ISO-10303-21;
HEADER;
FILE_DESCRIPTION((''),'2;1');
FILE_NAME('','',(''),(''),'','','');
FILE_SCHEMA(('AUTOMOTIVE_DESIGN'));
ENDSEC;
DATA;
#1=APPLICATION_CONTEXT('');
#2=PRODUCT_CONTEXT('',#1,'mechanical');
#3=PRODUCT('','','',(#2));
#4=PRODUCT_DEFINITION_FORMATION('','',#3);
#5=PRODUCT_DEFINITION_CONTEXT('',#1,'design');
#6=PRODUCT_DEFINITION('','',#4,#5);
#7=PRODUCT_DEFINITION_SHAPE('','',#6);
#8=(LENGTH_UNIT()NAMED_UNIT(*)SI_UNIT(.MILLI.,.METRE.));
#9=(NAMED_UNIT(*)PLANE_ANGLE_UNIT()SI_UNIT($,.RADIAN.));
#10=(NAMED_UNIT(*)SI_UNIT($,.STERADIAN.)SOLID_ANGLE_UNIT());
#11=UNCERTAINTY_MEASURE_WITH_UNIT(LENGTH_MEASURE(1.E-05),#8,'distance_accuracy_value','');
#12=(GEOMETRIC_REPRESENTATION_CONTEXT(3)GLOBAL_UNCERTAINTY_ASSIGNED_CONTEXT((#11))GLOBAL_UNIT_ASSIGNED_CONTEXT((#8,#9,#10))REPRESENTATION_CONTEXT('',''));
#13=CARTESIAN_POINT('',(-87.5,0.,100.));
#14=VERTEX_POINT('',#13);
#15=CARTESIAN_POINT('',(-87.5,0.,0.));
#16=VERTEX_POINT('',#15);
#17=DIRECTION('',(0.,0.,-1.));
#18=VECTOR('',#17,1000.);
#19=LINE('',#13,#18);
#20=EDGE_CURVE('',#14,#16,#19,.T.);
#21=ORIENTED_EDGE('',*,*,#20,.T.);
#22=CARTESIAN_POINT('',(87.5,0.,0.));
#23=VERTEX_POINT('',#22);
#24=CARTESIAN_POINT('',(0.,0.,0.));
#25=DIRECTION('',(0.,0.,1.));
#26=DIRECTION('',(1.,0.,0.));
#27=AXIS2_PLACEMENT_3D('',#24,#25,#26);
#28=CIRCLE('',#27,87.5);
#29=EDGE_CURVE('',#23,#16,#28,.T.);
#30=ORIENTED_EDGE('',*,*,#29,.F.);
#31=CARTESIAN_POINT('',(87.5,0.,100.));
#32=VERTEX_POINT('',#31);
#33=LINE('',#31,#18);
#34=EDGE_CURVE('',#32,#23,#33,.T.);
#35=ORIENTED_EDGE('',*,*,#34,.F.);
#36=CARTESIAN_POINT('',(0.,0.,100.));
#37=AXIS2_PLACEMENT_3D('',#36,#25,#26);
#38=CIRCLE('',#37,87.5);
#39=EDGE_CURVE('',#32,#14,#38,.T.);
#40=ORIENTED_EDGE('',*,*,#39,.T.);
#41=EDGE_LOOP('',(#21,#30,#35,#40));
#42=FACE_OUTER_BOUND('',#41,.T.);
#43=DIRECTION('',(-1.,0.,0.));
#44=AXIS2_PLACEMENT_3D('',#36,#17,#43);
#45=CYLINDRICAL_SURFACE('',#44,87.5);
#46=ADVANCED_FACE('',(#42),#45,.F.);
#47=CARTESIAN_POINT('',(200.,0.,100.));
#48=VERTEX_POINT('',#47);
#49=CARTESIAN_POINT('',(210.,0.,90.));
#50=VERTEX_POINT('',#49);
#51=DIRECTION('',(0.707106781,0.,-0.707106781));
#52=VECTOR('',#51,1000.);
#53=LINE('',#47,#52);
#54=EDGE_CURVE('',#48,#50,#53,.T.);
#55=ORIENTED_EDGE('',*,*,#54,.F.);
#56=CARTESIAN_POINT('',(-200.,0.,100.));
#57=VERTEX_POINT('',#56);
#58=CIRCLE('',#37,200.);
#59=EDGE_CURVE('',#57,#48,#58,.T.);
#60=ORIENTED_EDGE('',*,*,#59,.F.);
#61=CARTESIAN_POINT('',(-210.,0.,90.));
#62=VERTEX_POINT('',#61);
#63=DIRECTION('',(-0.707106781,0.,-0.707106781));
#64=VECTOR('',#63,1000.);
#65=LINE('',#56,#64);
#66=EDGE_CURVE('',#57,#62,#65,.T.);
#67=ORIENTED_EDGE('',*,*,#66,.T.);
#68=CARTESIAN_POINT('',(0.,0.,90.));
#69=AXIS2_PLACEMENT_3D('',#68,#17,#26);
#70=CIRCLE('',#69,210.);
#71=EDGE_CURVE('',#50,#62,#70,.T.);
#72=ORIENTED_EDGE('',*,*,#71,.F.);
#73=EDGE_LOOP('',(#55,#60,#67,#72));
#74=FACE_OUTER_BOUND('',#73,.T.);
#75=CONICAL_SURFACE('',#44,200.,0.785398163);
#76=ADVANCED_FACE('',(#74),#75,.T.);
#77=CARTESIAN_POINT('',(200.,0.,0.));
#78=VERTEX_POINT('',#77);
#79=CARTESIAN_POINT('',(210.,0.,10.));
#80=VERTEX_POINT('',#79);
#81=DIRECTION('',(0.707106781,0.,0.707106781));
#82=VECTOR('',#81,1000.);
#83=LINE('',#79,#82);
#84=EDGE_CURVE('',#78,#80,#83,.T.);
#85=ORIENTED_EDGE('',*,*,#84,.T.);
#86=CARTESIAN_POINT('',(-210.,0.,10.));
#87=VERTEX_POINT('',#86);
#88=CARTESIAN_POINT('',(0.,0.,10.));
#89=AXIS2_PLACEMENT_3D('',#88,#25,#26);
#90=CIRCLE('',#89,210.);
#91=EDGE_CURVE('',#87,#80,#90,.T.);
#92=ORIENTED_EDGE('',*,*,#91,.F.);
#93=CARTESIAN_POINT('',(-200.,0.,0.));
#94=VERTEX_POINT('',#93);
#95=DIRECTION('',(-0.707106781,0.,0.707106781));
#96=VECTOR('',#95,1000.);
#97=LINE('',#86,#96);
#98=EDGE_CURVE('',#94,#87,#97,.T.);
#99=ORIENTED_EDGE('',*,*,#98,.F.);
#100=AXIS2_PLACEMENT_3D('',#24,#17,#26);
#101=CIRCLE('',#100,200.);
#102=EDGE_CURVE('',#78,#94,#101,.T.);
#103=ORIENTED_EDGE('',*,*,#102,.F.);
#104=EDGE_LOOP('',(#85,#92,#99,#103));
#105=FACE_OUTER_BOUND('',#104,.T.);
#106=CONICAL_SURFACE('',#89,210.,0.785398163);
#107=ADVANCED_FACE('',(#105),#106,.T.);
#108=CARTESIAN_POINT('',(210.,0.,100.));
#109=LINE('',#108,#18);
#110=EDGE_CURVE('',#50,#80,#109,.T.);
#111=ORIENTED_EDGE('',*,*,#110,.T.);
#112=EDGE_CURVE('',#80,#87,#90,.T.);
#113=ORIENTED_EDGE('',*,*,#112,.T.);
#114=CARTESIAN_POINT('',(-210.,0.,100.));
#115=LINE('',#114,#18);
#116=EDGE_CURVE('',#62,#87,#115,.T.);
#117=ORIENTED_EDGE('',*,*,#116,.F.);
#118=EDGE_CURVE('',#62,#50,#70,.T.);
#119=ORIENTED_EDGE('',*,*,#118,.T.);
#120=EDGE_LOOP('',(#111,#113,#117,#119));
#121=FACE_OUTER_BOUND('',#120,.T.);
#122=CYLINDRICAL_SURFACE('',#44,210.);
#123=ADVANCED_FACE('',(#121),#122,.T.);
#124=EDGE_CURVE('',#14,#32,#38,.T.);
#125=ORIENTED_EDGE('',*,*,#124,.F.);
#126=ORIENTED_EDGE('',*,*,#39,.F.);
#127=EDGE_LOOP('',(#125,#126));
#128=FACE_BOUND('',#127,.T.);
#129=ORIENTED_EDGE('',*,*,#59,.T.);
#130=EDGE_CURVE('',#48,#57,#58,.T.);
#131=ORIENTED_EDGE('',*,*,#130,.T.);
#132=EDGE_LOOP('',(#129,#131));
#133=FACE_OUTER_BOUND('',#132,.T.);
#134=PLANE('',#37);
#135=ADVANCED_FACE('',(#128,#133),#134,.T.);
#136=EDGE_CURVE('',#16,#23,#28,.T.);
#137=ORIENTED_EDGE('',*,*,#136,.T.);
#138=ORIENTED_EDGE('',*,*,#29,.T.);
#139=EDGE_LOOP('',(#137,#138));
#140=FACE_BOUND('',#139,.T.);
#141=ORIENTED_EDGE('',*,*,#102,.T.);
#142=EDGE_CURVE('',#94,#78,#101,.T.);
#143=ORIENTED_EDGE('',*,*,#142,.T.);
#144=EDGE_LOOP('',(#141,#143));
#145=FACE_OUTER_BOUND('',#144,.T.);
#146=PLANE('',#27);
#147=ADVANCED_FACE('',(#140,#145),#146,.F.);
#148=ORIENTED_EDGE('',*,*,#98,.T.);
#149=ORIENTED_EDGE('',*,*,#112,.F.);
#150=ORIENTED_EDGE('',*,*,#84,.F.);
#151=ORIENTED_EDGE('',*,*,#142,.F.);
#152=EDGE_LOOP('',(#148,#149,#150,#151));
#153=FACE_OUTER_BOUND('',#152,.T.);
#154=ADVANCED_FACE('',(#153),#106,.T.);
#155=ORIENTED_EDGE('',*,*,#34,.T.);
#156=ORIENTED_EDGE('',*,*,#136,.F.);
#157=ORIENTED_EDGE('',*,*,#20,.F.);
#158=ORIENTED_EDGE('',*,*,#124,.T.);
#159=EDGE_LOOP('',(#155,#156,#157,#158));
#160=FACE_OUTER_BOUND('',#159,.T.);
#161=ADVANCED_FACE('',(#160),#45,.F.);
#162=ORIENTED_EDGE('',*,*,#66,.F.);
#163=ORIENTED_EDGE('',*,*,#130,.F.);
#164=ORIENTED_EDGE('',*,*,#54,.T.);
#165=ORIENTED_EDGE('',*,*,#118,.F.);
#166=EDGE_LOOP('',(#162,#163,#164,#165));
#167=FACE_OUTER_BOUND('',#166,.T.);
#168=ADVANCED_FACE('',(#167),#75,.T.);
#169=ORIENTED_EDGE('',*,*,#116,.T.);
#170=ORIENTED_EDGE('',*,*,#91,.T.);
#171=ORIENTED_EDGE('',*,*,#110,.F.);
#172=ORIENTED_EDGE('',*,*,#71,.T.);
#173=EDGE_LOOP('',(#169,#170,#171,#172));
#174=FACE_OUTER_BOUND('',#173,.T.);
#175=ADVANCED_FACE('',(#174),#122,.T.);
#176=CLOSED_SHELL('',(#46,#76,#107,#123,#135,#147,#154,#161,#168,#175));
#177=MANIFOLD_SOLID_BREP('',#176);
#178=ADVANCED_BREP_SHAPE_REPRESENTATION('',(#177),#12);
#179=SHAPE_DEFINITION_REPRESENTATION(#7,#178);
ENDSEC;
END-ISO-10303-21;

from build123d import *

# Parameters (mm, degrees)
SKETCH1_R           = 210
SKETCH1_R_2         = 87.5
BOSS_EXTRUDE1_DEPTH = 100
CHAMFER1_SIZE       = 10


with BuildPart() as part:
    # Sketch1 → Boss-Extrude1 (new body)
    with BuildSketch(Plane.XY):
        Circle(SKETCH1_R)
        Circle(SKETCH1_R_2, mode=Mode.SUBTRACT)
    extrude(amount=BOSS_EXTRUDE1_DEPTH)

    # Chamfer1
    chamfer1_edges = [part.edges().sort_by_distance(p)[0] for p in [
        (-210, 0, 0),
        (-210, 0, 100),
    ]]
    chamfer(chamfer1_edges, length=CHAMFER1_SIZE)


solid = part.part
